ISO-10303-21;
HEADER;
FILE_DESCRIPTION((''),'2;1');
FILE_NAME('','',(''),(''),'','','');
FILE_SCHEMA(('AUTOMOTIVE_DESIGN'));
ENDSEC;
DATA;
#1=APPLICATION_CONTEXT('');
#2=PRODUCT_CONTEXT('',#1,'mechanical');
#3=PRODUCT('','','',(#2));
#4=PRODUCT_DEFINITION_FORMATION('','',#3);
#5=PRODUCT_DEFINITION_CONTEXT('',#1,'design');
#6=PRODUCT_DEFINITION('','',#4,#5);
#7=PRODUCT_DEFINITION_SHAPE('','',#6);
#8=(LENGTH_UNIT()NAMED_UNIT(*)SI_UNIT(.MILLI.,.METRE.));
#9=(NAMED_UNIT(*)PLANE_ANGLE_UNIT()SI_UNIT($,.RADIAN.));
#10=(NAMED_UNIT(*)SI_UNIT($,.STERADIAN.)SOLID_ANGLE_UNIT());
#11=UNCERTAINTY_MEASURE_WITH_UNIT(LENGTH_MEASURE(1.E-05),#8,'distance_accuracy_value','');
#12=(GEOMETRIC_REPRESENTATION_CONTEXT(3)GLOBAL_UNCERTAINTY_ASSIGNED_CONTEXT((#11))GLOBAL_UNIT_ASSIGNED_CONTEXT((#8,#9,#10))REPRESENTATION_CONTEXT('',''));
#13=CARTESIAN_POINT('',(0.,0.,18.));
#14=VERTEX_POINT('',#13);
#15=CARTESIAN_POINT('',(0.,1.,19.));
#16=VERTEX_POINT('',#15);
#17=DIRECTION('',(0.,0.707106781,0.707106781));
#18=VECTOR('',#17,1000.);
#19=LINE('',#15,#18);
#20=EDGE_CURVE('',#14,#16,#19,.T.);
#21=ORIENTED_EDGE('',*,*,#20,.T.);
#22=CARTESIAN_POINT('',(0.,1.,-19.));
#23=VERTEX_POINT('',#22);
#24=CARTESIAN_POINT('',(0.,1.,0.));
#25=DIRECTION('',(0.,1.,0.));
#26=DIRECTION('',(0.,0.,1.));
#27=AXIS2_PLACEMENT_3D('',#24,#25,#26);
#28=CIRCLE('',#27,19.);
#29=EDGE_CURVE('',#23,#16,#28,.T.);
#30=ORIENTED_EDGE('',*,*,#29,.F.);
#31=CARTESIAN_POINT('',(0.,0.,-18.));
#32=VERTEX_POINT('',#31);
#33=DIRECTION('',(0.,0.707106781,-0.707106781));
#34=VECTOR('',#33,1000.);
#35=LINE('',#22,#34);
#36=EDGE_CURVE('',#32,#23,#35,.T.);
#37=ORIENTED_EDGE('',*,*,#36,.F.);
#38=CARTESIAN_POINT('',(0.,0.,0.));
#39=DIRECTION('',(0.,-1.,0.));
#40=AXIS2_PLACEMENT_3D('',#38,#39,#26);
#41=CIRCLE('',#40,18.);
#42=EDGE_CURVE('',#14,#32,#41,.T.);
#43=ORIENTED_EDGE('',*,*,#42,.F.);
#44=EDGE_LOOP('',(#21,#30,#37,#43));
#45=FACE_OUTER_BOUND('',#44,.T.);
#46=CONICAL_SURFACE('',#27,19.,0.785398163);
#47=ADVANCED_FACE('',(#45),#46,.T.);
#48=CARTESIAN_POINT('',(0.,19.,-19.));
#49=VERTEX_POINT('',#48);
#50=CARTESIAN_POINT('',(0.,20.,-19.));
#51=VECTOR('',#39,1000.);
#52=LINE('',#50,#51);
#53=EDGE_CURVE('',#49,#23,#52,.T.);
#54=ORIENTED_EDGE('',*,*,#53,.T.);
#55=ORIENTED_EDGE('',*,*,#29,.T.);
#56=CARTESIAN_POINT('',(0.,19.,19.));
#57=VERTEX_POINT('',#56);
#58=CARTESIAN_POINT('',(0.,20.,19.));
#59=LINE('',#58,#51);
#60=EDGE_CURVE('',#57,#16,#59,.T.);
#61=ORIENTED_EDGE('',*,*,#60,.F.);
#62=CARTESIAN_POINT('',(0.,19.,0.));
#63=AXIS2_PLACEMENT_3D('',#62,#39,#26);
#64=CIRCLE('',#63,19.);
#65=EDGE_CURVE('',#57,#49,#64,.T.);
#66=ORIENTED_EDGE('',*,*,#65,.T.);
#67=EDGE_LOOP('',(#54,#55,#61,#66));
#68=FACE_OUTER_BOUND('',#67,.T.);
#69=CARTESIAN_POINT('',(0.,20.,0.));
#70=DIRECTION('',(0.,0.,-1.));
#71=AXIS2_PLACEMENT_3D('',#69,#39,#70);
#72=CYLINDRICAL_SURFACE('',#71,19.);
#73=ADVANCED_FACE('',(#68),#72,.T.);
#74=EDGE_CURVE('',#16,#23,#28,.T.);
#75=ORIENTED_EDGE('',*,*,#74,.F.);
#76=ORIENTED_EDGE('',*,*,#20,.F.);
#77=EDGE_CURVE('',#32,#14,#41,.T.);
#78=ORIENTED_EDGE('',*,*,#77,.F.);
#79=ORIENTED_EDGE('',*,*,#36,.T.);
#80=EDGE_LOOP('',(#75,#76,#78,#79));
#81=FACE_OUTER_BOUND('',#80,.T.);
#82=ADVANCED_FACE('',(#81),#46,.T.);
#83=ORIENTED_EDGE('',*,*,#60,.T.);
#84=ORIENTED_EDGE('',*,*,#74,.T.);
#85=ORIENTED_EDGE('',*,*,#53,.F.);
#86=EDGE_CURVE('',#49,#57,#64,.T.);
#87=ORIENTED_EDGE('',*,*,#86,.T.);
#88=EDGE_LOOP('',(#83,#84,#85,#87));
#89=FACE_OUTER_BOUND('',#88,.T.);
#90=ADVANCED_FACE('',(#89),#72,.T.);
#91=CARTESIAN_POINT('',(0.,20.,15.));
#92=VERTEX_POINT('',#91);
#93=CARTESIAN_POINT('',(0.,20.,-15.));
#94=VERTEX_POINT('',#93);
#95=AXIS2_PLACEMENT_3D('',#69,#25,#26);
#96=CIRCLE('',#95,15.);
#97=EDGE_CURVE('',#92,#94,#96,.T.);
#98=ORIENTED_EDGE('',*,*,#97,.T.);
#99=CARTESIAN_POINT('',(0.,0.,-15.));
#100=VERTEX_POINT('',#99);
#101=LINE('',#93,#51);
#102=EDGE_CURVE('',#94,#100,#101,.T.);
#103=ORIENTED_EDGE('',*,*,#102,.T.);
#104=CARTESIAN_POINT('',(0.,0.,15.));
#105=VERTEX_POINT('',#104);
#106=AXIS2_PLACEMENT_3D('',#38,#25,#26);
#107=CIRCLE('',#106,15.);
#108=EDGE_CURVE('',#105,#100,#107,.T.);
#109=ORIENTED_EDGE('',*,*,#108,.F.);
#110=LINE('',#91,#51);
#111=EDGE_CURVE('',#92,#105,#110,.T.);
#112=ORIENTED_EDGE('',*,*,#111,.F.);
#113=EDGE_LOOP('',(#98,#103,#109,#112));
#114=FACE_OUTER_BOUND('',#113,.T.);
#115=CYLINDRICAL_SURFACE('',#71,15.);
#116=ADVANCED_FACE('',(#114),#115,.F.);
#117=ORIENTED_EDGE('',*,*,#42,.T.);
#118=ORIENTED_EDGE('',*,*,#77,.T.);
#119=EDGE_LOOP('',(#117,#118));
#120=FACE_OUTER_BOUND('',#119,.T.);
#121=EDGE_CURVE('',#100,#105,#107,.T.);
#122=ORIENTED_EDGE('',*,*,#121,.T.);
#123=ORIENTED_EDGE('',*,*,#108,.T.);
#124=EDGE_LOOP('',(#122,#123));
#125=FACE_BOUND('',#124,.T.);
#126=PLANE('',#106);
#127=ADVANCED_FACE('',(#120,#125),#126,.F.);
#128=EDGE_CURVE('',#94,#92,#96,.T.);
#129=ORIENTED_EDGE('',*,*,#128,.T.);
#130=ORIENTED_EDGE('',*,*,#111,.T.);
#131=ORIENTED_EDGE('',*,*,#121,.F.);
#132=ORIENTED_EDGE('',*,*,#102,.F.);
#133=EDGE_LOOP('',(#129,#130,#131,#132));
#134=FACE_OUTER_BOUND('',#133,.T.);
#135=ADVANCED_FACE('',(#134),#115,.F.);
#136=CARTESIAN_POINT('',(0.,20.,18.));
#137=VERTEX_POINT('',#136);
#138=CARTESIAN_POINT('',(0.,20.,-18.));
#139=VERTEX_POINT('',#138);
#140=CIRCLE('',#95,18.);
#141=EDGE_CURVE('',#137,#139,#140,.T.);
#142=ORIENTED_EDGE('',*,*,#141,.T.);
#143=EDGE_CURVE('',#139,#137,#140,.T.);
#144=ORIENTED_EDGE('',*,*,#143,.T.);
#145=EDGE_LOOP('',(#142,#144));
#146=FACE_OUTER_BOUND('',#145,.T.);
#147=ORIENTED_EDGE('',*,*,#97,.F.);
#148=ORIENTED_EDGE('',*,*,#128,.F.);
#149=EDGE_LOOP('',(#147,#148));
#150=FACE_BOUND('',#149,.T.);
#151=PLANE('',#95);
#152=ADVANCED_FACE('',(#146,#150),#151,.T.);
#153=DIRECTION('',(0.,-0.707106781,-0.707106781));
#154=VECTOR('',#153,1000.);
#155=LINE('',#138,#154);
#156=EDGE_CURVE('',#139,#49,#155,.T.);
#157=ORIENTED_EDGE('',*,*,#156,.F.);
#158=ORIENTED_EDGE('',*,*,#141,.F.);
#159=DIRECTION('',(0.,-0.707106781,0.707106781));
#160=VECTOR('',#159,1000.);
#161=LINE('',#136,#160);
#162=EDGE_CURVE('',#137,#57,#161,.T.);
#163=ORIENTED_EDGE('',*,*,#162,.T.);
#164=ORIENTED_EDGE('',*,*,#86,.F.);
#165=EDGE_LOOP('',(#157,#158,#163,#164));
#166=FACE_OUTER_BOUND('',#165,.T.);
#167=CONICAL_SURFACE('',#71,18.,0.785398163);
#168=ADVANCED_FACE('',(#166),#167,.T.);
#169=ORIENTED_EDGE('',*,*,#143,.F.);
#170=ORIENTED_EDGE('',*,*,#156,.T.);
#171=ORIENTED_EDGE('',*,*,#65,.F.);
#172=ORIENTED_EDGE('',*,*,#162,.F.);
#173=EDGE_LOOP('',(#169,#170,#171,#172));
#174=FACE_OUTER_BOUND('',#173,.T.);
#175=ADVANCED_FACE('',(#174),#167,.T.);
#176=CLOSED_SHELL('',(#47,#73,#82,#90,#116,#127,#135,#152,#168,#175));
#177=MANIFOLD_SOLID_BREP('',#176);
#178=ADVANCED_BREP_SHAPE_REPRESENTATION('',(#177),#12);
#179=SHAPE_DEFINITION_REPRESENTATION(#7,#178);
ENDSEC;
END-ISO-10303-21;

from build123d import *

# Parameters (mm, degrees)
SKETCH1_R           = 19
SKETCH1_R_2         = 15
BOSS_EXTRUDE1_DEPTH = 20
CHAMFER1_SIZE       = 1


with BuildPart() as part:
    # Sketch1 → Boss-Extrude1 (new body)
    with BuildSketch(Plane(origin=(0, 0, 0), x_dir=(1, 0, 0), z_dir=(0, 1, 0))):
        with Locations(Location((0, 0, 0), (0, 0, 270))):
            Circle(SKETCH1_R)
        with Locations(Location((0, 0, 0), (0, 0, 270))):
            Circle(SKETCH1_R_2, mode=Mode.SUBTRACT)
    extrude(amount=BOSS_EXTRUDE1_DEPTH)

    # Chamfer1
    chamfer1_edges = [part.edges().sort_by_distance(p)[0] for p in [
        (0, 0, -19),
        (0, 20, -19),
    ]]
    chamfer(chamfer1_edges, length=CHAMFER1_SIZE)


solid = part.part
